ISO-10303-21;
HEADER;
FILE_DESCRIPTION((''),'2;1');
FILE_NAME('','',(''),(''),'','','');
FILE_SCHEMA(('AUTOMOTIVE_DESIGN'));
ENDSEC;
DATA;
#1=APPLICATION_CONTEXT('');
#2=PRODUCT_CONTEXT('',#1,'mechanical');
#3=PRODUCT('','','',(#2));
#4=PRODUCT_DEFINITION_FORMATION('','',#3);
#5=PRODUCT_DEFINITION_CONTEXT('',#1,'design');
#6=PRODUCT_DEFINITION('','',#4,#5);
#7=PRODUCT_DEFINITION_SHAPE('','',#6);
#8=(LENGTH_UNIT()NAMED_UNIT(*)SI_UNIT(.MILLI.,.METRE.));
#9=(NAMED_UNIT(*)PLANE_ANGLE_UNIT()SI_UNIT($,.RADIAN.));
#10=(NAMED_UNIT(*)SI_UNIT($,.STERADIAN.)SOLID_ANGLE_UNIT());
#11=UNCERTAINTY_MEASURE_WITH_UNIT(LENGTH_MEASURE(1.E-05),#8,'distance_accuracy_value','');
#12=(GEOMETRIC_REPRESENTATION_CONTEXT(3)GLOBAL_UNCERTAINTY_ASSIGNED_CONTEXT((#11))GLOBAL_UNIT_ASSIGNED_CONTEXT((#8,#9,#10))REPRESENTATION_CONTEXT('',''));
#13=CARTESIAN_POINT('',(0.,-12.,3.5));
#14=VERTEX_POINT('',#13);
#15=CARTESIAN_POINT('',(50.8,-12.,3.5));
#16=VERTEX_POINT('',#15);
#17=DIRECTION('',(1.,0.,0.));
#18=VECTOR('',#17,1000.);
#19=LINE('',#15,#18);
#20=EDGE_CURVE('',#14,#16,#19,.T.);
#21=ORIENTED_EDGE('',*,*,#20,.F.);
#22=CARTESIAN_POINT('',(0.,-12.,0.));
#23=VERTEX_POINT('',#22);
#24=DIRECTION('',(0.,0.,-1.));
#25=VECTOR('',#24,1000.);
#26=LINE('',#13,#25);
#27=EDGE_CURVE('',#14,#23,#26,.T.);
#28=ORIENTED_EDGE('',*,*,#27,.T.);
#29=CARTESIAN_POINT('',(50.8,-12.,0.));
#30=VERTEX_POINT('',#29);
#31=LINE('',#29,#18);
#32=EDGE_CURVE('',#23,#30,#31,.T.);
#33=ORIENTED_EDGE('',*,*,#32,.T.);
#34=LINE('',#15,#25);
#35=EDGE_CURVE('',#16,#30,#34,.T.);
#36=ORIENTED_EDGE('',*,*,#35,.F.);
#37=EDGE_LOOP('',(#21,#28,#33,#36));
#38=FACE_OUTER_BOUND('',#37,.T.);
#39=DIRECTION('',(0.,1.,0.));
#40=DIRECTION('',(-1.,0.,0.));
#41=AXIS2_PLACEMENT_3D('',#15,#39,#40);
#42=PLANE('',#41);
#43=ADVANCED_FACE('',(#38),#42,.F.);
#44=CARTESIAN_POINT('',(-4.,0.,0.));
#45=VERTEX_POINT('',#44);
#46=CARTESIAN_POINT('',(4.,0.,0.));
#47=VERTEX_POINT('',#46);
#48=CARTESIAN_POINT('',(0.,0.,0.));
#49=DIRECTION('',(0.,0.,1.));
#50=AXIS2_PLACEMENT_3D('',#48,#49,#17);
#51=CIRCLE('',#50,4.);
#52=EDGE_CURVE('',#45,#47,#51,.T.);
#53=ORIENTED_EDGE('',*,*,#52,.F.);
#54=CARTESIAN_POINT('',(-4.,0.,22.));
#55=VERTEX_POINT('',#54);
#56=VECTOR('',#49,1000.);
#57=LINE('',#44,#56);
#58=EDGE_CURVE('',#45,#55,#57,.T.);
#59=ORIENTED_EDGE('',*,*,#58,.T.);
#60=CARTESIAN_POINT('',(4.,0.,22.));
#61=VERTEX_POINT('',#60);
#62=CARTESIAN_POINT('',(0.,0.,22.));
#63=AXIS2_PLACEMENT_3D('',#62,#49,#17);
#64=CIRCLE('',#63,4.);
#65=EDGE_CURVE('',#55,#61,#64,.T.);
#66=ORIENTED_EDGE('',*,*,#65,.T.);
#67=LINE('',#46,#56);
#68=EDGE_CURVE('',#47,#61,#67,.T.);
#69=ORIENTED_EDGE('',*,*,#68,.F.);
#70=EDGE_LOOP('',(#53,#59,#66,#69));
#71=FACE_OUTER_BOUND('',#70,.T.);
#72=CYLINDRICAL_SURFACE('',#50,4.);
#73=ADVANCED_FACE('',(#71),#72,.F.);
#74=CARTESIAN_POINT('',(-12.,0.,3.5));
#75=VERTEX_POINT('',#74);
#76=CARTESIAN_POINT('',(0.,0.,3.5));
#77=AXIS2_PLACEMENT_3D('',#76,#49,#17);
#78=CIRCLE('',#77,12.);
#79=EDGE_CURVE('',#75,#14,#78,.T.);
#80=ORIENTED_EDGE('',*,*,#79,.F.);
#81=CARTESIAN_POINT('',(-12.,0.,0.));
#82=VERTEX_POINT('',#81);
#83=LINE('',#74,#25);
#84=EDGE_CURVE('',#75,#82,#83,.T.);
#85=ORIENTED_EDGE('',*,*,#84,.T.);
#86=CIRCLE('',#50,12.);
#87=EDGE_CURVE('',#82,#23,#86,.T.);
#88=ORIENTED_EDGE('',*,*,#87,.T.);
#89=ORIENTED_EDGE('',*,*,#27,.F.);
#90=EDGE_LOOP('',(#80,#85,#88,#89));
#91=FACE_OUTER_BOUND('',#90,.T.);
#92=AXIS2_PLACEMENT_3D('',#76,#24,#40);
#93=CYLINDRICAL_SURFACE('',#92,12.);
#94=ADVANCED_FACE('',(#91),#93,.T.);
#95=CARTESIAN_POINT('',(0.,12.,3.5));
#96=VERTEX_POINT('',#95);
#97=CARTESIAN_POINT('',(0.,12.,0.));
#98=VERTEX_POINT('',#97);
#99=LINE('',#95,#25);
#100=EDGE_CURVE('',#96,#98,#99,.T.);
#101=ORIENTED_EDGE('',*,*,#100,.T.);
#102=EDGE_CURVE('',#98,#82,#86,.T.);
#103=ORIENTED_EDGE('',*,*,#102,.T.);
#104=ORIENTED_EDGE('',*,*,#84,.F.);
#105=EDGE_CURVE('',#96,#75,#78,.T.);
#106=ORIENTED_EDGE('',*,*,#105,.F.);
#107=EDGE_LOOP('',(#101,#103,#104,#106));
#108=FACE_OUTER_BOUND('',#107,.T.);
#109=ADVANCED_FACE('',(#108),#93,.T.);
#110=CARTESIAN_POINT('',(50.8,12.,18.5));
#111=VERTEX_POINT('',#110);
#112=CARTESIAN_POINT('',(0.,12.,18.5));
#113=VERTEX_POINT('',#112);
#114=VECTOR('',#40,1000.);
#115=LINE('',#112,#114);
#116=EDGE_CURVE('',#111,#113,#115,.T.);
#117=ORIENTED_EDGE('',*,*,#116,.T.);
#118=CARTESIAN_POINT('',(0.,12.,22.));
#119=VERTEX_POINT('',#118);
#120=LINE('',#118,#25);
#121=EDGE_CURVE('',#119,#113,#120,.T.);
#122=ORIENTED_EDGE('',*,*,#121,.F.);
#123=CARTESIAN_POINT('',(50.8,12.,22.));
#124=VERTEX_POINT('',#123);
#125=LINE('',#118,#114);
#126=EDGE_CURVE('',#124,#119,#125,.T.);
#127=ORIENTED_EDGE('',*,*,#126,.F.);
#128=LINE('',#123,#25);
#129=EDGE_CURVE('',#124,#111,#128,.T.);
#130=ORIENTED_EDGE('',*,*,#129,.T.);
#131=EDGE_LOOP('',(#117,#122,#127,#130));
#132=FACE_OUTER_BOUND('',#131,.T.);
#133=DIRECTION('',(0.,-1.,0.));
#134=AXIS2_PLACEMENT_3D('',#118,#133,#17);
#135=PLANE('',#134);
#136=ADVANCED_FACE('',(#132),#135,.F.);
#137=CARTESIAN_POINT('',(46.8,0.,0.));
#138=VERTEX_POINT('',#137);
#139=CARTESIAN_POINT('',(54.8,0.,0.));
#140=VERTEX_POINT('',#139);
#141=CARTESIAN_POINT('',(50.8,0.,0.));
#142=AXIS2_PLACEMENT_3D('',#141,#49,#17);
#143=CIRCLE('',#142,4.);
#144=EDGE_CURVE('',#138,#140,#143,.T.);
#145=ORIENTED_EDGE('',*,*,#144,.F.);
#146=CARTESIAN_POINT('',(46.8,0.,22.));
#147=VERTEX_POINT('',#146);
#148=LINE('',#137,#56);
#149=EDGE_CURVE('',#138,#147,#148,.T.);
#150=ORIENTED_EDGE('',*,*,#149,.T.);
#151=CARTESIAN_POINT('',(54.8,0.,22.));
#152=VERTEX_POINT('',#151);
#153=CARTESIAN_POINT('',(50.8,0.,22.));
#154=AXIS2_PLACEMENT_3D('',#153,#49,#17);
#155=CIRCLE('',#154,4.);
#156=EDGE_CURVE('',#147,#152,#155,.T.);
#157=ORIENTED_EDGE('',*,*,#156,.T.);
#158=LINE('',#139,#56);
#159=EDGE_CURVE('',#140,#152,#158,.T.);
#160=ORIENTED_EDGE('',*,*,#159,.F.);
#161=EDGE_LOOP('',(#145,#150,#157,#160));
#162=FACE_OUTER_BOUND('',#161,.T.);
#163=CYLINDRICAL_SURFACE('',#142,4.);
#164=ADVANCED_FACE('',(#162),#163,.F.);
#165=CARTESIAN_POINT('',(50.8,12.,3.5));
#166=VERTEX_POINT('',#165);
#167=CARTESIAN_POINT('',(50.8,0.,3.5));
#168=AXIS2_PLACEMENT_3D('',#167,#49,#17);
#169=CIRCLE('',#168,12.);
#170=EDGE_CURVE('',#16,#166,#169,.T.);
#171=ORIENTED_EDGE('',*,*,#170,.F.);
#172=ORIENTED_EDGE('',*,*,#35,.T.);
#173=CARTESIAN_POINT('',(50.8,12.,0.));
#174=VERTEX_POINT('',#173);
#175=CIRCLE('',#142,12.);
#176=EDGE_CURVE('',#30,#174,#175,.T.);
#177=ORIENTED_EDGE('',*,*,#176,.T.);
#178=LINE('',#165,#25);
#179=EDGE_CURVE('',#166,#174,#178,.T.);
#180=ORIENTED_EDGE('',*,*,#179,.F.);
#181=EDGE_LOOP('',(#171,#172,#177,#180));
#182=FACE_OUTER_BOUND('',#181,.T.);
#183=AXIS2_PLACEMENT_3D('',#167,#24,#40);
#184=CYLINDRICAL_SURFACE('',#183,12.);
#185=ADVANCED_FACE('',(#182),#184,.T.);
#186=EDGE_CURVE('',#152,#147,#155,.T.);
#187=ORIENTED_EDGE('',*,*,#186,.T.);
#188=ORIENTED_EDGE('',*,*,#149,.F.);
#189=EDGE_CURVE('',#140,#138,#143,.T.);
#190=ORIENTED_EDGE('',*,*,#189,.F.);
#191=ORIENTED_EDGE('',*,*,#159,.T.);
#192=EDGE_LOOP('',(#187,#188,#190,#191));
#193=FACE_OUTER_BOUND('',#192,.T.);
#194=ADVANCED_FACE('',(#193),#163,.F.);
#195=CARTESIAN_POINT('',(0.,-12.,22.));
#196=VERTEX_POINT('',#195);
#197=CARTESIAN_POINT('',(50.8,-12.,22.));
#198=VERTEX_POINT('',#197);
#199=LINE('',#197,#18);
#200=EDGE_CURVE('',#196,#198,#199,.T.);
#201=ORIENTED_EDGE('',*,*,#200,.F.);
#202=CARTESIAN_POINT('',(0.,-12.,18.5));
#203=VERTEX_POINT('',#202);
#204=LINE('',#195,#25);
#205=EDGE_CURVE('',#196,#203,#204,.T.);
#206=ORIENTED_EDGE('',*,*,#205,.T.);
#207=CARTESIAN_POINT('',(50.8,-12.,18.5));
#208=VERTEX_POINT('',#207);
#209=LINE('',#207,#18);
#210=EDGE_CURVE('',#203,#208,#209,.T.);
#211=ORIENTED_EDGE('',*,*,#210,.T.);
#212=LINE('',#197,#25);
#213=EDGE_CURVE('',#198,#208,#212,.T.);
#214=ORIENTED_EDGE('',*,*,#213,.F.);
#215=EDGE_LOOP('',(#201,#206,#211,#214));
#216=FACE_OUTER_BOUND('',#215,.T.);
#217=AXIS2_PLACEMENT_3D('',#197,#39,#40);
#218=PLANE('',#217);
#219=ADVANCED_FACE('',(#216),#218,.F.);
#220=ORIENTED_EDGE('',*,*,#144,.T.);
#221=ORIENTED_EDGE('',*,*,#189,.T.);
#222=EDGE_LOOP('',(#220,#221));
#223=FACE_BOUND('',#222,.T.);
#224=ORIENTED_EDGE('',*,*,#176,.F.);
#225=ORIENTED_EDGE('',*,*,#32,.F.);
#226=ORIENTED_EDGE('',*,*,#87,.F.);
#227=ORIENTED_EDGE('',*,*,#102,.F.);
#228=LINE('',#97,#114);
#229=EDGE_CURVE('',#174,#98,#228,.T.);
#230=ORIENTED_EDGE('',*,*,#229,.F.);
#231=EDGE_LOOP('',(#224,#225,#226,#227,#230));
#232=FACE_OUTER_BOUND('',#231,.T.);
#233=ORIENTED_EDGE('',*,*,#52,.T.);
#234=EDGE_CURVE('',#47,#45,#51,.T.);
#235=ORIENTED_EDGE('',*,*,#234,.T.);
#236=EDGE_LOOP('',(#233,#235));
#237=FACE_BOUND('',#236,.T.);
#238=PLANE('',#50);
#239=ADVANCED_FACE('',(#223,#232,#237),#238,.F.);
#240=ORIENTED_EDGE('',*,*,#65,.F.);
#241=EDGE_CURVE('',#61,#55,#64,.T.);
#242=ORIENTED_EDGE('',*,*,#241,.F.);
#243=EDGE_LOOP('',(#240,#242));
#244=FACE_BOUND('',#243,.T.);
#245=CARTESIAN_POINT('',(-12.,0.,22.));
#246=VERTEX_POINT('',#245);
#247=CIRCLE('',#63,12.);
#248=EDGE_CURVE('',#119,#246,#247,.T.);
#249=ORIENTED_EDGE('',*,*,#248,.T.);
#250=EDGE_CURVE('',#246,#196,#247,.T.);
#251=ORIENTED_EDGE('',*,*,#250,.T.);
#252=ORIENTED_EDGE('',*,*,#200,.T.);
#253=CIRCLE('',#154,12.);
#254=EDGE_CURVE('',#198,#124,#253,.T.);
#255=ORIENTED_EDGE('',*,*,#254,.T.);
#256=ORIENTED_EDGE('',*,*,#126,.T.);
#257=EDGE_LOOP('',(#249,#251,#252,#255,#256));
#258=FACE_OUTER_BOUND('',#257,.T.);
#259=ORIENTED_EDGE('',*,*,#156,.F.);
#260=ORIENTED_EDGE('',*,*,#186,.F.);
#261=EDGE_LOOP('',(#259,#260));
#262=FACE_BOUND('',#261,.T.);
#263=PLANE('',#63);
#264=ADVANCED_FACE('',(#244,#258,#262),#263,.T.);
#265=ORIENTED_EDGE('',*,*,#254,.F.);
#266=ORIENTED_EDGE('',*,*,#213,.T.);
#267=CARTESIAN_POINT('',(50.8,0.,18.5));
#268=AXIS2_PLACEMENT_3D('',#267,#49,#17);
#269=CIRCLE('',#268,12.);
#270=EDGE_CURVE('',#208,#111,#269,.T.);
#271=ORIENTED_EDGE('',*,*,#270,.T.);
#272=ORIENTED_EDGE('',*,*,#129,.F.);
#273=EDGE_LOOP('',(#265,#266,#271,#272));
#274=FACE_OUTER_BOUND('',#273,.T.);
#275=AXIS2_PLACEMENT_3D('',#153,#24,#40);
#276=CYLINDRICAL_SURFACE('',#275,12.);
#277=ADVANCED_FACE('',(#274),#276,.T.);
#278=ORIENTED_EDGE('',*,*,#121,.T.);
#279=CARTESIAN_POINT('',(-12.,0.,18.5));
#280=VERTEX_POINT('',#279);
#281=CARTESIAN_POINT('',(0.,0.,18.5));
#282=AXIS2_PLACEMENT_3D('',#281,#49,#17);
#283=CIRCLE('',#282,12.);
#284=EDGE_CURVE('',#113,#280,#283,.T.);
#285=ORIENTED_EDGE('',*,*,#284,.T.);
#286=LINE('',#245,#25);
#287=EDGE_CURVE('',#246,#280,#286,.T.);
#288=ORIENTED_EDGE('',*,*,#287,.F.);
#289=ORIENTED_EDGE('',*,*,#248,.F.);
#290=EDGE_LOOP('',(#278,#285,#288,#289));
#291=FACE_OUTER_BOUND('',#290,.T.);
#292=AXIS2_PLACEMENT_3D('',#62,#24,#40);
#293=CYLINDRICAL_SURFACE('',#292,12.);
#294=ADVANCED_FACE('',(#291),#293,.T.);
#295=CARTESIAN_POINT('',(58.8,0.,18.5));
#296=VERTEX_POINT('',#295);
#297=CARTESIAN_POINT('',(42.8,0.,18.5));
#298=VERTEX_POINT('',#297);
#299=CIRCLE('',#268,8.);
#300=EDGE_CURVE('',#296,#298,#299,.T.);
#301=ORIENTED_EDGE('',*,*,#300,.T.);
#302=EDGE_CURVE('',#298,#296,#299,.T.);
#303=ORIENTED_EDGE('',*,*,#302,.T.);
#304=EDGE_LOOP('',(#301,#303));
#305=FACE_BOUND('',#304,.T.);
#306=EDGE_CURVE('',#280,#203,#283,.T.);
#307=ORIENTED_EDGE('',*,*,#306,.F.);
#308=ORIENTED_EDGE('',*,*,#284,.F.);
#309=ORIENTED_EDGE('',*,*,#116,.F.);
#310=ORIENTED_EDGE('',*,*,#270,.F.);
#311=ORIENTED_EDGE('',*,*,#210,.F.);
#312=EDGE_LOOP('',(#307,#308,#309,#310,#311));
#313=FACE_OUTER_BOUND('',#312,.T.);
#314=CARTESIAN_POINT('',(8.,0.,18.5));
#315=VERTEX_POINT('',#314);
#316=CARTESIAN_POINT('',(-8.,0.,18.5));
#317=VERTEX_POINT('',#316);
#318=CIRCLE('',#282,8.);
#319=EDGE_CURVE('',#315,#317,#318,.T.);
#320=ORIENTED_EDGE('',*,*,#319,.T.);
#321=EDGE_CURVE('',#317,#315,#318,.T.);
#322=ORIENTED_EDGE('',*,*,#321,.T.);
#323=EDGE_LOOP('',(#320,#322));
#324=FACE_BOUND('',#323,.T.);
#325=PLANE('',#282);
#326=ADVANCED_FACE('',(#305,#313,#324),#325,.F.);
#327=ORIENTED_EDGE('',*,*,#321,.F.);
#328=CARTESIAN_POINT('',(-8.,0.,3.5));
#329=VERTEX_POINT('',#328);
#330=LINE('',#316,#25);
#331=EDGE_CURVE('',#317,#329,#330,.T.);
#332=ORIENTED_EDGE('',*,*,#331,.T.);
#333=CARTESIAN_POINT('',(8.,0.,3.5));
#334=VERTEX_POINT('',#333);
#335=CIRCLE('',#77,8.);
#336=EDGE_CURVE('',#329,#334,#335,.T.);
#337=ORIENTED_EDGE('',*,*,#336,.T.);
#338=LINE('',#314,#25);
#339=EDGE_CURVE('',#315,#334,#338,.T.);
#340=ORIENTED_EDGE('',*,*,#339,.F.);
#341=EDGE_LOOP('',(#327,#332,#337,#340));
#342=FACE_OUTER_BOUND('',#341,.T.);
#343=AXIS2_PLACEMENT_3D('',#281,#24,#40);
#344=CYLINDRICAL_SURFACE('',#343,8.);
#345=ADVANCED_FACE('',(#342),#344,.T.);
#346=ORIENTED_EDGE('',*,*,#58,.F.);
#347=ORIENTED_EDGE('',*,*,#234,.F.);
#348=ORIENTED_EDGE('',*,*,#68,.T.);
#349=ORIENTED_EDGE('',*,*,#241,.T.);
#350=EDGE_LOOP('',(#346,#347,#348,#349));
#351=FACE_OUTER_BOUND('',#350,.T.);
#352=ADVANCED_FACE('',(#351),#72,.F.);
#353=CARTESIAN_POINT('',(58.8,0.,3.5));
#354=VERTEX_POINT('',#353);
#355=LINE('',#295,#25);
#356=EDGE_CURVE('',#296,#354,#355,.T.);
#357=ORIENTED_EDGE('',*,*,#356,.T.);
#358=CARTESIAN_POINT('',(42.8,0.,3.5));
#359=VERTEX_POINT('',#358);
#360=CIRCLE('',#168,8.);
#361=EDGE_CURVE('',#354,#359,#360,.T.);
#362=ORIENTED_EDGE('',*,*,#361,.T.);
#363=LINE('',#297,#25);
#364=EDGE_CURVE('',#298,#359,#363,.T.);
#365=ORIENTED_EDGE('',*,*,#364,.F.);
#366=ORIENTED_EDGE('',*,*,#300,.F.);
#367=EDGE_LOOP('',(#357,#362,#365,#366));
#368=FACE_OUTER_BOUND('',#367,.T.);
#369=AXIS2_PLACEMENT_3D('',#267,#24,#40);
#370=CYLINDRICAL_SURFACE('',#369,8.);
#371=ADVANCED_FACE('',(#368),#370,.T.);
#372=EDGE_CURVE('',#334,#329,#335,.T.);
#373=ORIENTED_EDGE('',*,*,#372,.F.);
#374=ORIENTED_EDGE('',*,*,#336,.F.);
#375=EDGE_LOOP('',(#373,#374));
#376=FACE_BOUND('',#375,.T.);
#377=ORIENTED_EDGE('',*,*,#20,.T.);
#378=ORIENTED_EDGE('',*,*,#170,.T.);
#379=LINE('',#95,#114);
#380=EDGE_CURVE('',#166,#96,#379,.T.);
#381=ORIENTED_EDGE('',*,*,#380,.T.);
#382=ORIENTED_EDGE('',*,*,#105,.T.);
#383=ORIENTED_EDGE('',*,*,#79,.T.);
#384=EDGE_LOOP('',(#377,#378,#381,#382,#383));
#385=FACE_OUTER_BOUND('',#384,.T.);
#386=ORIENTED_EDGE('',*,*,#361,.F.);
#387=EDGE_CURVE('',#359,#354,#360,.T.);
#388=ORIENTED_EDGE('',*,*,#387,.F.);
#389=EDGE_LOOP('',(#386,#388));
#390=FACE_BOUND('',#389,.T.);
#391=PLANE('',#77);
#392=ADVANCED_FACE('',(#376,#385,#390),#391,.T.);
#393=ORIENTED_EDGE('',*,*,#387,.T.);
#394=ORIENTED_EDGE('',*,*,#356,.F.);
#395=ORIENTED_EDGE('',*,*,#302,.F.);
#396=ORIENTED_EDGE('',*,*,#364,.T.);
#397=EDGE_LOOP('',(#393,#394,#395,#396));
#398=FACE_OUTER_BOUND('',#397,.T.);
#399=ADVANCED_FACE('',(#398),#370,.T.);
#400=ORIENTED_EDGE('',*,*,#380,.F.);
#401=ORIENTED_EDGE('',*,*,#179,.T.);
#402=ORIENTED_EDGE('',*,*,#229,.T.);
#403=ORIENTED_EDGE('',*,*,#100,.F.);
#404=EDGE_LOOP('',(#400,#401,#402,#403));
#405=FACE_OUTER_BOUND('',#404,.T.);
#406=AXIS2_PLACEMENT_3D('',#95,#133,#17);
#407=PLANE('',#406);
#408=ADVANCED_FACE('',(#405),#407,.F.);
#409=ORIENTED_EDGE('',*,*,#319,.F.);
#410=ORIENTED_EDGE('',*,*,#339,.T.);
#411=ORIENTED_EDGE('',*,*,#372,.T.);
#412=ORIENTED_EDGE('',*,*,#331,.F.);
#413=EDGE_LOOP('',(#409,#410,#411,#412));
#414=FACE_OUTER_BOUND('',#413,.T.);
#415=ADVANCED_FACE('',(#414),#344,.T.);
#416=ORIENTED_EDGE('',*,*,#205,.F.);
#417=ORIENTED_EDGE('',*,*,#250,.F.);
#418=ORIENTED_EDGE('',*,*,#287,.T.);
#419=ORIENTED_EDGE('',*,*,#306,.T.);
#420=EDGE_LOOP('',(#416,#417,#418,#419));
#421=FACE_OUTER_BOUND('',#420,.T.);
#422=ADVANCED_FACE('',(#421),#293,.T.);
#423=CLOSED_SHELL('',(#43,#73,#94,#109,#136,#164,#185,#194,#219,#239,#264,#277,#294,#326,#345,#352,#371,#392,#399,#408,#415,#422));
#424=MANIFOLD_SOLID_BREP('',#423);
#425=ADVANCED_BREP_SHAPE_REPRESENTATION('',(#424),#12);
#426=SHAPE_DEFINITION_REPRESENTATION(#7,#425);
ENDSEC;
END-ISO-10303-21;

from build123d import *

# Parameters (mm, degrees)
REAR_LINK_PLATE_DEPTH  = 3.5
ROLLER_PROFILES_R      = 8
ROLLERS_2X_16_DEPTH    = 15
FRONT_LINK_PLATE_DEPTH = 3.5
PIN_BORE_PROFILES_R    = 4
PIN_BORES_2X_8_DEPTH   = 22


with BuildPart() as part:
    # Rear Plate Profile → Rear Link Plate (new body)
    with BuildSketch(Plane.XY):
        with BuildLine():
            Line((0, 12), (50.8, 12))
            ThreePointArc((50.8, 12), (62.8, 0), (50.8, -12))
            Line((50.8, -12), (0, -12))
            ThreePointArc((0, -12), (-12, 0), (0, 12))
        make_face()
    extrude(amount=REAR_LINK_PLATE_DEPTH)

    # Roller Profiles → Rollers 2xØ16 (add)
    with BuildSketch(Plane.XY.offset(3.5)):
        Circle(ROLLER_PROFILES_R)
        with Locations((50.8, 0)):
            Circle(ROLLER_PROFILES_R)
    extrude(amount=ROLLERS_2X_16_DEPTH)

    # Front Plate Profile → Front Link Plate (add)
    with BuildSketch(Plane.XY.offset(18.5)):
        with BuildLine():
            Line((0, 12), (50.8, 12))
            ThreePointArc((50.8, 12), (62.8, 0), (50.8, -12))
            Line((50.8, -12), (0, -12))
            ThreePointArc((0, -12), (-12, 0), (0, 12))
        make_face()
    extrude(amount=FRONT_LINK_PLATE_DEPTH)

    # Pin Bore Profiles → Pin Bores 2xØ8 (cut)
    with BuildSketch(Plane.XY.offset(22)):
        Circle(PIN_BORE_PROFILES_R)
        with Locations((50.8, 0)):
            Circle(PIN_BORE_PROFILES_R)
    extrude(amount=-PIN_BORES_2X_8_DEPTH, mode=Mode.SUBTRACT)


solid = part.part
